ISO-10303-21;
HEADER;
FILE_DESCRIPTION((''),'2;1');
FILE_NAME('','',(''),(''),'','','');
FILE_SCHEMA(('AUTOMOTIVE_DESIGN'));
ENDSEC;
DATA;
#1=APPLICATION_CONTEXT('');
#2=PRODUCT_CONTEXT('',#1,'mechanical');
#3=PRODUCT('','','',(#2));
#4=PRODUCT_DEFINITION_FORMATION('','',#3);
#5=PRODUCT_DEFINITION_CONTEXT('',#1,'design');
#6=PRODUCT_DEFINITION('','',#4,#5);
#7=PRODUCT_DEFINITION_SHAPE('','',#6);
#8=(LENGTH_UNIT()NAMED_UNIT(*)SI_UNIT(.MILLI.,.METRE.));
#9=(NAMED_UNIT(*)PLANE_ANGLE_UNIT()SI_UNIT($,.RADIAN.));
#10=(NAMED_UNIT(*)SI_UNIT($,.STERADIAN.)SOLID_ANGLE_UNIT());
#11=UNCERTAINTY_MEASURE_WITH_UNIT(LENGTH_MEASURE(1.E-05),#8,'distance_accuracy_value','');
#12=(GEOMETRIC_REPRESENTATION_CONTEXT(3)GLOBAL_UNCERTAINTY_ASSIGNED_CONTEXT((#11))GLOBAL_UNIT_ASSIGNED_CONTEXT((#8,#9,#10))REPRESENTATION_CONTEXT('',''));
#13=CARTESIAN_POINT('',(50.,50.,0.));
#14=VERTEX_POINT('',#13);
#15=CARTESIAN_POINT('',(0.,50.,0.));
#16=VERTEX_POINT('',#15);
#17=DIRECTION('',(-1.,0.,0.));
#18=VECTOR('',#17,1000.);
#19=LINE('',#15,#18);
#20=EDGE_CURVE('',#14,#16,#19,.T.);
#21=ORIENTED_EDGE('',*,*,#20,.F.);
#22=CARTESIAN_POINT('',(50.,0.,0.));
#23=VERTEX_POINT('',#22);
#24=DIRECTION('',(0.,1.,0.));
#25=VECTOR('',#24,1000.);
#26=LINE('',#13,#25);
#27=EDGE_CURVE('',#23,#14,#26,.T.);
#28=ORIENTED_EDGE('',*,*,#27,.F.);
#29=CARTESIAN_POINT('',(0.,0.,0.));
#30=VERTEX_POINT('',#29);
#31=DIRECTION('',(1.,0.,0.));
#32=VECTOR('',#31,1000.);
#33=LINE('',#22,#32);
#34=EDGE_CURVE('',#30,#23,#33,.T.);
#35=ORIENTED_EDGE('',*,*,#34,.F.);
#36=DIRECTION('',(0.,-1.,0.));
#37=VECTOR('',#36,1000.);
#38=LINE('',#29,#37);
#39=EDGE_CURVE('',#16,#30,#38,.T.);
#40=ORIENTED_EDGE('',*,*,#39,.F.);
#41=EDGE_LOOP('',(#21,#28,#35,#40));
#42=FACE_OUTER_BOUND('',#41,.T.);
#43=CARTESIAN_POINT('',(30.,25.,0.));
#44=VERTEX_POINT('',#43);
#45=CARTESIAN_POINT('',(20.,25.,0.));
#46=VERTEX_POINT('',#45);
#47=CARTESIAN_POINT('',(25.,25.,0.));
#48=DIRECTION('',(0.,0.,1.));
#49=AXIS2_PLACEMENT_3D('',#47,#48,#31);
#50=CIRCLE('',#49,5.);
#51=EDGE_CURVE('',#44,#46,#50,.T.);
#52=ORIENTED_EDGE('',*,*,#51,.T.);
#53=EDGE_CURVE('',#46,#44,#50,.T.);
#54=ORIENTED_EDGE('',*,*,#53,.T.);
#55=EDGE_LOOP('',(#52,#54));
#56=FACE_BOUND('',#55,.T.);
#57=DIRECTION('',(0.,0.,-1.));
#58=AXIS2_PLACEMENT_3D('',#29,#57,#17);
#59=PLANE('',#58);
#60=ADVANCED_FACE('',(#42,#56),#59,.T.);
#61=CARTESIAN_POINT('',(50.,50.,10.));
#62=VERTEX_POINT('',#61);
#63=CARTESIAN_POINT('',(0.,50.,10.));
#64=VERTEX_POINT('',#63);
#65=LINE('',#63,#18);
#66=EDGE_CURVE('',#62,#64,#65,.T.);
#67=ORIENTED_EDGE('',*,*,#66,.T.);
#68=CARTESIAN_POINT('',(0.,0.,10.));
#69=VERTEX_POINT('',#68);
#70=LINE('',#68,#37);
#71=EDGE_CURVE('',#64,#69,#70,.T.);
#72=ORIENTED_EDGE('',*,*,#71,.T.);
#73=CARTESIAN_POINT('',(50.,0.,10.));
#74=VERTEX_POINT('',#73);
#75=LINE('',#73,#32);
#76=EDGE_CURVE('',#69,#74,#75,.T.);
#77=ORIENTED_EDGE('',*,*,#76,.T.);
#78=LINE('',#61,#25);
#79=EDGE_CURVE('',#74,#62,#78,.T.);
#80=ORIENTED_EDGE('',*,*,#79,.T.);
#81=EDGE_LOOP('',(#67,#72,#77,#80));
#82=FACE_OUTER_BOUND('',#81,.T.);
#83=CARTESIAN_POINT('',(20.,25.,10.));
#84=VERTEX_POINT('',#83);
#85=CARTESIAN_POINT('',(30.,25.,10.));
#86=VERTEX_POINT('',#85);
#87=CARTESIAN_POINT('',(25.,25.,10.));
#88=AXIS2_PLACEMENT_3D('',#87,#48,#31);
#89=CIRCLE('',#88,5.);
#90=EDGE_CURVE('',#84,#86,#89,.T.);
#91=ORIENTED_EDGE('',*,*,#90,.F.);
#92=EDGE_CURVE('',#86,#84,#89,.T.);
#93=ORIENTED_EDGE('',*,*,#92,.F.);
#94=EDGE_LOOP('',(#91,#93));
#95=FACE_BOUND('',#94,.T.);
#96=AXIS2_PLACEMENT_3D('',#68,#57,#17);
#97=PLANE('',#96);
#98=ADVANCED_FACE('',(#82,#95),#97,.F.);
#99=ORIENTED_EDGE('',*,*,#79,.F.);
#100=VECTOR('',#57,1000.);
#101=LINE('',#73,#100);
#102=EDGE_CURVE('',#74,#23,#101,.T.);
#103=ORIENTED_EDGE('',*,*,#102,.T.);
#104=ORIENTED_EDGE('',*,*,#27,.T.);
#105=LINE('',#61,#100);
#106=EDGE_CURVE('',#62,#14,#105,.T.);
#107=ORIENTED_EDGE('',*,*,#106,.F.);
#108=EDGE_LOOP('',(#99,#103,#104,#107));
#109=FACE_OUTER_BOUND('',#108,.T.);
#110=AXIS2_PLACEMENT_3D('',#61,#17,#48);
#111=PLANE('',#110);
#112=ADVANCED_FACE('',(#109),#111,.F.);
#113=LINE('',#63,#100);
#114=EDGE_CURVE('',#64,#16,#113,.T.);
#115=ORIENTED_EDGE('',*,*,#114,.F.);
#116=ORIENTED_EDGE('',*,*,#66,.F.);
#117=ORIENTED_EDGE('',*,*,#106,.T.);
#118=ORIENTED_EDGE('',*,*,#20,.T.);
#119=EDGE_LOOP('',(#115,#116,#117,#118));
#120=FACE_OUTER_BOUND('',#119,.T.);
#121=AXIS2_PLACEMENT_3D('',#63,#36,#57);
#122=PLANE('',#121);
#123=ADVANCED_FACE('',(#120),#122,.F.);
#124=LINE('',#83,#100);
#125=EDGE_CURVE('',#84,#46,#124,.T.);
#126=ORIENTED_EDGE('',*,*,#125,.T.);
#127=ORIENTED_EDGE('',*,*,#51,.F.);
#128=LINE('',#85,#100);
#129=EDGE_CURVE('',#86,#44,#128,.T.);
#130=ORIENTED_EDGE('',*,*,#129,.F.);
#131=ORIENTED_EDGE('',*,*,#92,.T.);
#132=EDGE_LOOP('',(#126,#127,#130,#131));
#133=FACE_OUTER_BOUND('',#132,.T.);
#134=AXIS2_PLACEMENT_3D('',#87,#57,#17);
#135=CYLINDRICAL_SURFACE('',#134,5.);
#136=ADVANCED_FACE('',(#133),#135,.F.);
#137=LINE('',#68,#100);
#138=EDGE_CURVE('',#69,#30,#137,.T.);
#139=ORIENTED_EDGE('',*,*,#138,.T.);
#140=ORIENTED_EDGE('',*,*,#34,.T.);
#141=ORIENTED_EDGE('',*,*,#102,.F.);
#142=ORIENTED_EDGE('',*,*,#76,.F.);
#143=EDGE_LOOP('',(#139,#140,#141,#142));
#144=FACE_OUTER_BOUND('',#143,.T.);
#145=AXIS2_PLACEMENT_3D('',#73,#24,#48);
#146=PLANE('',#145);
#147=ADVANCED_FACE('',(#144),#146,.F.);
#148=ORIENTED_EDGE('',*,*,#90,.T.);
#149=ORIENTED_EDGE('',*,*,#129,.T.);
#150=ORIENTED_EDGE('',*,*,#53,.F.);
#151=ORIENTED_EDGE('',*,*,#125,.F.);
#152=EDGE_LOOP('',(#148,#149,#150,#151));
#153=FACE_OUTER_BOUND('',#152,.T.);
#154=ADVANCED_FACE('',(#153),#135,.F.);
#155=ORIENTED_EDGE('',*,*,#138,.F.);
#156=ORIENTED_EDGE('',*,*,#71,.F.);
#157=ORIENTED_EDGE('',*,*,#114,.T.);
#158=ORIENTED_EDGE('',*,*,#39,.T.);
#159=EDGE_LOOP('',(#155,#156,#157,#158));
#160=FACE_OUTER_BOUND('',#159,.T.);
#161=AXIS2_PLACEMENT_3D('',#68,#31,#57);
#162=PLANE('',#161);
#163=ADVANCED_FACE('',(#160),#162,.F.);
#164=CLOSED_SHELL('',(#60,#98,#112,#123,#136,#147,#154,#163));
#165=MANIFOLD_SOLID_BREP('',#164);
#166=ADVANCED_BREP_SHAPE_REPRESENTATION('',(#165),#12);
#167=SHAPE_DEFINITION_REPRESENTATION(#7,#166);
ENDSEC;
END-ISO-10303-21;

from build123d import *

# Parameters (mm, degrees)
SKETCH_1_W      = 50
SKETCH_1_H      = 50
SKETCH_1_R      = 5
EXTRUDE_1_DEPTH = 10


with BuildPart() as part:
    # 草图1 → 凸台-拉伸1 (new body)
    with BuildSketch(Plane.XY):
        with Locations((25, 25)):
            Rectangle(SKETCH_1_W, SKETCH_1_H)
        with Locations((25, 25)):
            Circle(SKETCH_1_R, mode=Mode.SUBTRACT)
    extrude(amount=EXTRUDE_1_DEPTH)


solid = part.part
